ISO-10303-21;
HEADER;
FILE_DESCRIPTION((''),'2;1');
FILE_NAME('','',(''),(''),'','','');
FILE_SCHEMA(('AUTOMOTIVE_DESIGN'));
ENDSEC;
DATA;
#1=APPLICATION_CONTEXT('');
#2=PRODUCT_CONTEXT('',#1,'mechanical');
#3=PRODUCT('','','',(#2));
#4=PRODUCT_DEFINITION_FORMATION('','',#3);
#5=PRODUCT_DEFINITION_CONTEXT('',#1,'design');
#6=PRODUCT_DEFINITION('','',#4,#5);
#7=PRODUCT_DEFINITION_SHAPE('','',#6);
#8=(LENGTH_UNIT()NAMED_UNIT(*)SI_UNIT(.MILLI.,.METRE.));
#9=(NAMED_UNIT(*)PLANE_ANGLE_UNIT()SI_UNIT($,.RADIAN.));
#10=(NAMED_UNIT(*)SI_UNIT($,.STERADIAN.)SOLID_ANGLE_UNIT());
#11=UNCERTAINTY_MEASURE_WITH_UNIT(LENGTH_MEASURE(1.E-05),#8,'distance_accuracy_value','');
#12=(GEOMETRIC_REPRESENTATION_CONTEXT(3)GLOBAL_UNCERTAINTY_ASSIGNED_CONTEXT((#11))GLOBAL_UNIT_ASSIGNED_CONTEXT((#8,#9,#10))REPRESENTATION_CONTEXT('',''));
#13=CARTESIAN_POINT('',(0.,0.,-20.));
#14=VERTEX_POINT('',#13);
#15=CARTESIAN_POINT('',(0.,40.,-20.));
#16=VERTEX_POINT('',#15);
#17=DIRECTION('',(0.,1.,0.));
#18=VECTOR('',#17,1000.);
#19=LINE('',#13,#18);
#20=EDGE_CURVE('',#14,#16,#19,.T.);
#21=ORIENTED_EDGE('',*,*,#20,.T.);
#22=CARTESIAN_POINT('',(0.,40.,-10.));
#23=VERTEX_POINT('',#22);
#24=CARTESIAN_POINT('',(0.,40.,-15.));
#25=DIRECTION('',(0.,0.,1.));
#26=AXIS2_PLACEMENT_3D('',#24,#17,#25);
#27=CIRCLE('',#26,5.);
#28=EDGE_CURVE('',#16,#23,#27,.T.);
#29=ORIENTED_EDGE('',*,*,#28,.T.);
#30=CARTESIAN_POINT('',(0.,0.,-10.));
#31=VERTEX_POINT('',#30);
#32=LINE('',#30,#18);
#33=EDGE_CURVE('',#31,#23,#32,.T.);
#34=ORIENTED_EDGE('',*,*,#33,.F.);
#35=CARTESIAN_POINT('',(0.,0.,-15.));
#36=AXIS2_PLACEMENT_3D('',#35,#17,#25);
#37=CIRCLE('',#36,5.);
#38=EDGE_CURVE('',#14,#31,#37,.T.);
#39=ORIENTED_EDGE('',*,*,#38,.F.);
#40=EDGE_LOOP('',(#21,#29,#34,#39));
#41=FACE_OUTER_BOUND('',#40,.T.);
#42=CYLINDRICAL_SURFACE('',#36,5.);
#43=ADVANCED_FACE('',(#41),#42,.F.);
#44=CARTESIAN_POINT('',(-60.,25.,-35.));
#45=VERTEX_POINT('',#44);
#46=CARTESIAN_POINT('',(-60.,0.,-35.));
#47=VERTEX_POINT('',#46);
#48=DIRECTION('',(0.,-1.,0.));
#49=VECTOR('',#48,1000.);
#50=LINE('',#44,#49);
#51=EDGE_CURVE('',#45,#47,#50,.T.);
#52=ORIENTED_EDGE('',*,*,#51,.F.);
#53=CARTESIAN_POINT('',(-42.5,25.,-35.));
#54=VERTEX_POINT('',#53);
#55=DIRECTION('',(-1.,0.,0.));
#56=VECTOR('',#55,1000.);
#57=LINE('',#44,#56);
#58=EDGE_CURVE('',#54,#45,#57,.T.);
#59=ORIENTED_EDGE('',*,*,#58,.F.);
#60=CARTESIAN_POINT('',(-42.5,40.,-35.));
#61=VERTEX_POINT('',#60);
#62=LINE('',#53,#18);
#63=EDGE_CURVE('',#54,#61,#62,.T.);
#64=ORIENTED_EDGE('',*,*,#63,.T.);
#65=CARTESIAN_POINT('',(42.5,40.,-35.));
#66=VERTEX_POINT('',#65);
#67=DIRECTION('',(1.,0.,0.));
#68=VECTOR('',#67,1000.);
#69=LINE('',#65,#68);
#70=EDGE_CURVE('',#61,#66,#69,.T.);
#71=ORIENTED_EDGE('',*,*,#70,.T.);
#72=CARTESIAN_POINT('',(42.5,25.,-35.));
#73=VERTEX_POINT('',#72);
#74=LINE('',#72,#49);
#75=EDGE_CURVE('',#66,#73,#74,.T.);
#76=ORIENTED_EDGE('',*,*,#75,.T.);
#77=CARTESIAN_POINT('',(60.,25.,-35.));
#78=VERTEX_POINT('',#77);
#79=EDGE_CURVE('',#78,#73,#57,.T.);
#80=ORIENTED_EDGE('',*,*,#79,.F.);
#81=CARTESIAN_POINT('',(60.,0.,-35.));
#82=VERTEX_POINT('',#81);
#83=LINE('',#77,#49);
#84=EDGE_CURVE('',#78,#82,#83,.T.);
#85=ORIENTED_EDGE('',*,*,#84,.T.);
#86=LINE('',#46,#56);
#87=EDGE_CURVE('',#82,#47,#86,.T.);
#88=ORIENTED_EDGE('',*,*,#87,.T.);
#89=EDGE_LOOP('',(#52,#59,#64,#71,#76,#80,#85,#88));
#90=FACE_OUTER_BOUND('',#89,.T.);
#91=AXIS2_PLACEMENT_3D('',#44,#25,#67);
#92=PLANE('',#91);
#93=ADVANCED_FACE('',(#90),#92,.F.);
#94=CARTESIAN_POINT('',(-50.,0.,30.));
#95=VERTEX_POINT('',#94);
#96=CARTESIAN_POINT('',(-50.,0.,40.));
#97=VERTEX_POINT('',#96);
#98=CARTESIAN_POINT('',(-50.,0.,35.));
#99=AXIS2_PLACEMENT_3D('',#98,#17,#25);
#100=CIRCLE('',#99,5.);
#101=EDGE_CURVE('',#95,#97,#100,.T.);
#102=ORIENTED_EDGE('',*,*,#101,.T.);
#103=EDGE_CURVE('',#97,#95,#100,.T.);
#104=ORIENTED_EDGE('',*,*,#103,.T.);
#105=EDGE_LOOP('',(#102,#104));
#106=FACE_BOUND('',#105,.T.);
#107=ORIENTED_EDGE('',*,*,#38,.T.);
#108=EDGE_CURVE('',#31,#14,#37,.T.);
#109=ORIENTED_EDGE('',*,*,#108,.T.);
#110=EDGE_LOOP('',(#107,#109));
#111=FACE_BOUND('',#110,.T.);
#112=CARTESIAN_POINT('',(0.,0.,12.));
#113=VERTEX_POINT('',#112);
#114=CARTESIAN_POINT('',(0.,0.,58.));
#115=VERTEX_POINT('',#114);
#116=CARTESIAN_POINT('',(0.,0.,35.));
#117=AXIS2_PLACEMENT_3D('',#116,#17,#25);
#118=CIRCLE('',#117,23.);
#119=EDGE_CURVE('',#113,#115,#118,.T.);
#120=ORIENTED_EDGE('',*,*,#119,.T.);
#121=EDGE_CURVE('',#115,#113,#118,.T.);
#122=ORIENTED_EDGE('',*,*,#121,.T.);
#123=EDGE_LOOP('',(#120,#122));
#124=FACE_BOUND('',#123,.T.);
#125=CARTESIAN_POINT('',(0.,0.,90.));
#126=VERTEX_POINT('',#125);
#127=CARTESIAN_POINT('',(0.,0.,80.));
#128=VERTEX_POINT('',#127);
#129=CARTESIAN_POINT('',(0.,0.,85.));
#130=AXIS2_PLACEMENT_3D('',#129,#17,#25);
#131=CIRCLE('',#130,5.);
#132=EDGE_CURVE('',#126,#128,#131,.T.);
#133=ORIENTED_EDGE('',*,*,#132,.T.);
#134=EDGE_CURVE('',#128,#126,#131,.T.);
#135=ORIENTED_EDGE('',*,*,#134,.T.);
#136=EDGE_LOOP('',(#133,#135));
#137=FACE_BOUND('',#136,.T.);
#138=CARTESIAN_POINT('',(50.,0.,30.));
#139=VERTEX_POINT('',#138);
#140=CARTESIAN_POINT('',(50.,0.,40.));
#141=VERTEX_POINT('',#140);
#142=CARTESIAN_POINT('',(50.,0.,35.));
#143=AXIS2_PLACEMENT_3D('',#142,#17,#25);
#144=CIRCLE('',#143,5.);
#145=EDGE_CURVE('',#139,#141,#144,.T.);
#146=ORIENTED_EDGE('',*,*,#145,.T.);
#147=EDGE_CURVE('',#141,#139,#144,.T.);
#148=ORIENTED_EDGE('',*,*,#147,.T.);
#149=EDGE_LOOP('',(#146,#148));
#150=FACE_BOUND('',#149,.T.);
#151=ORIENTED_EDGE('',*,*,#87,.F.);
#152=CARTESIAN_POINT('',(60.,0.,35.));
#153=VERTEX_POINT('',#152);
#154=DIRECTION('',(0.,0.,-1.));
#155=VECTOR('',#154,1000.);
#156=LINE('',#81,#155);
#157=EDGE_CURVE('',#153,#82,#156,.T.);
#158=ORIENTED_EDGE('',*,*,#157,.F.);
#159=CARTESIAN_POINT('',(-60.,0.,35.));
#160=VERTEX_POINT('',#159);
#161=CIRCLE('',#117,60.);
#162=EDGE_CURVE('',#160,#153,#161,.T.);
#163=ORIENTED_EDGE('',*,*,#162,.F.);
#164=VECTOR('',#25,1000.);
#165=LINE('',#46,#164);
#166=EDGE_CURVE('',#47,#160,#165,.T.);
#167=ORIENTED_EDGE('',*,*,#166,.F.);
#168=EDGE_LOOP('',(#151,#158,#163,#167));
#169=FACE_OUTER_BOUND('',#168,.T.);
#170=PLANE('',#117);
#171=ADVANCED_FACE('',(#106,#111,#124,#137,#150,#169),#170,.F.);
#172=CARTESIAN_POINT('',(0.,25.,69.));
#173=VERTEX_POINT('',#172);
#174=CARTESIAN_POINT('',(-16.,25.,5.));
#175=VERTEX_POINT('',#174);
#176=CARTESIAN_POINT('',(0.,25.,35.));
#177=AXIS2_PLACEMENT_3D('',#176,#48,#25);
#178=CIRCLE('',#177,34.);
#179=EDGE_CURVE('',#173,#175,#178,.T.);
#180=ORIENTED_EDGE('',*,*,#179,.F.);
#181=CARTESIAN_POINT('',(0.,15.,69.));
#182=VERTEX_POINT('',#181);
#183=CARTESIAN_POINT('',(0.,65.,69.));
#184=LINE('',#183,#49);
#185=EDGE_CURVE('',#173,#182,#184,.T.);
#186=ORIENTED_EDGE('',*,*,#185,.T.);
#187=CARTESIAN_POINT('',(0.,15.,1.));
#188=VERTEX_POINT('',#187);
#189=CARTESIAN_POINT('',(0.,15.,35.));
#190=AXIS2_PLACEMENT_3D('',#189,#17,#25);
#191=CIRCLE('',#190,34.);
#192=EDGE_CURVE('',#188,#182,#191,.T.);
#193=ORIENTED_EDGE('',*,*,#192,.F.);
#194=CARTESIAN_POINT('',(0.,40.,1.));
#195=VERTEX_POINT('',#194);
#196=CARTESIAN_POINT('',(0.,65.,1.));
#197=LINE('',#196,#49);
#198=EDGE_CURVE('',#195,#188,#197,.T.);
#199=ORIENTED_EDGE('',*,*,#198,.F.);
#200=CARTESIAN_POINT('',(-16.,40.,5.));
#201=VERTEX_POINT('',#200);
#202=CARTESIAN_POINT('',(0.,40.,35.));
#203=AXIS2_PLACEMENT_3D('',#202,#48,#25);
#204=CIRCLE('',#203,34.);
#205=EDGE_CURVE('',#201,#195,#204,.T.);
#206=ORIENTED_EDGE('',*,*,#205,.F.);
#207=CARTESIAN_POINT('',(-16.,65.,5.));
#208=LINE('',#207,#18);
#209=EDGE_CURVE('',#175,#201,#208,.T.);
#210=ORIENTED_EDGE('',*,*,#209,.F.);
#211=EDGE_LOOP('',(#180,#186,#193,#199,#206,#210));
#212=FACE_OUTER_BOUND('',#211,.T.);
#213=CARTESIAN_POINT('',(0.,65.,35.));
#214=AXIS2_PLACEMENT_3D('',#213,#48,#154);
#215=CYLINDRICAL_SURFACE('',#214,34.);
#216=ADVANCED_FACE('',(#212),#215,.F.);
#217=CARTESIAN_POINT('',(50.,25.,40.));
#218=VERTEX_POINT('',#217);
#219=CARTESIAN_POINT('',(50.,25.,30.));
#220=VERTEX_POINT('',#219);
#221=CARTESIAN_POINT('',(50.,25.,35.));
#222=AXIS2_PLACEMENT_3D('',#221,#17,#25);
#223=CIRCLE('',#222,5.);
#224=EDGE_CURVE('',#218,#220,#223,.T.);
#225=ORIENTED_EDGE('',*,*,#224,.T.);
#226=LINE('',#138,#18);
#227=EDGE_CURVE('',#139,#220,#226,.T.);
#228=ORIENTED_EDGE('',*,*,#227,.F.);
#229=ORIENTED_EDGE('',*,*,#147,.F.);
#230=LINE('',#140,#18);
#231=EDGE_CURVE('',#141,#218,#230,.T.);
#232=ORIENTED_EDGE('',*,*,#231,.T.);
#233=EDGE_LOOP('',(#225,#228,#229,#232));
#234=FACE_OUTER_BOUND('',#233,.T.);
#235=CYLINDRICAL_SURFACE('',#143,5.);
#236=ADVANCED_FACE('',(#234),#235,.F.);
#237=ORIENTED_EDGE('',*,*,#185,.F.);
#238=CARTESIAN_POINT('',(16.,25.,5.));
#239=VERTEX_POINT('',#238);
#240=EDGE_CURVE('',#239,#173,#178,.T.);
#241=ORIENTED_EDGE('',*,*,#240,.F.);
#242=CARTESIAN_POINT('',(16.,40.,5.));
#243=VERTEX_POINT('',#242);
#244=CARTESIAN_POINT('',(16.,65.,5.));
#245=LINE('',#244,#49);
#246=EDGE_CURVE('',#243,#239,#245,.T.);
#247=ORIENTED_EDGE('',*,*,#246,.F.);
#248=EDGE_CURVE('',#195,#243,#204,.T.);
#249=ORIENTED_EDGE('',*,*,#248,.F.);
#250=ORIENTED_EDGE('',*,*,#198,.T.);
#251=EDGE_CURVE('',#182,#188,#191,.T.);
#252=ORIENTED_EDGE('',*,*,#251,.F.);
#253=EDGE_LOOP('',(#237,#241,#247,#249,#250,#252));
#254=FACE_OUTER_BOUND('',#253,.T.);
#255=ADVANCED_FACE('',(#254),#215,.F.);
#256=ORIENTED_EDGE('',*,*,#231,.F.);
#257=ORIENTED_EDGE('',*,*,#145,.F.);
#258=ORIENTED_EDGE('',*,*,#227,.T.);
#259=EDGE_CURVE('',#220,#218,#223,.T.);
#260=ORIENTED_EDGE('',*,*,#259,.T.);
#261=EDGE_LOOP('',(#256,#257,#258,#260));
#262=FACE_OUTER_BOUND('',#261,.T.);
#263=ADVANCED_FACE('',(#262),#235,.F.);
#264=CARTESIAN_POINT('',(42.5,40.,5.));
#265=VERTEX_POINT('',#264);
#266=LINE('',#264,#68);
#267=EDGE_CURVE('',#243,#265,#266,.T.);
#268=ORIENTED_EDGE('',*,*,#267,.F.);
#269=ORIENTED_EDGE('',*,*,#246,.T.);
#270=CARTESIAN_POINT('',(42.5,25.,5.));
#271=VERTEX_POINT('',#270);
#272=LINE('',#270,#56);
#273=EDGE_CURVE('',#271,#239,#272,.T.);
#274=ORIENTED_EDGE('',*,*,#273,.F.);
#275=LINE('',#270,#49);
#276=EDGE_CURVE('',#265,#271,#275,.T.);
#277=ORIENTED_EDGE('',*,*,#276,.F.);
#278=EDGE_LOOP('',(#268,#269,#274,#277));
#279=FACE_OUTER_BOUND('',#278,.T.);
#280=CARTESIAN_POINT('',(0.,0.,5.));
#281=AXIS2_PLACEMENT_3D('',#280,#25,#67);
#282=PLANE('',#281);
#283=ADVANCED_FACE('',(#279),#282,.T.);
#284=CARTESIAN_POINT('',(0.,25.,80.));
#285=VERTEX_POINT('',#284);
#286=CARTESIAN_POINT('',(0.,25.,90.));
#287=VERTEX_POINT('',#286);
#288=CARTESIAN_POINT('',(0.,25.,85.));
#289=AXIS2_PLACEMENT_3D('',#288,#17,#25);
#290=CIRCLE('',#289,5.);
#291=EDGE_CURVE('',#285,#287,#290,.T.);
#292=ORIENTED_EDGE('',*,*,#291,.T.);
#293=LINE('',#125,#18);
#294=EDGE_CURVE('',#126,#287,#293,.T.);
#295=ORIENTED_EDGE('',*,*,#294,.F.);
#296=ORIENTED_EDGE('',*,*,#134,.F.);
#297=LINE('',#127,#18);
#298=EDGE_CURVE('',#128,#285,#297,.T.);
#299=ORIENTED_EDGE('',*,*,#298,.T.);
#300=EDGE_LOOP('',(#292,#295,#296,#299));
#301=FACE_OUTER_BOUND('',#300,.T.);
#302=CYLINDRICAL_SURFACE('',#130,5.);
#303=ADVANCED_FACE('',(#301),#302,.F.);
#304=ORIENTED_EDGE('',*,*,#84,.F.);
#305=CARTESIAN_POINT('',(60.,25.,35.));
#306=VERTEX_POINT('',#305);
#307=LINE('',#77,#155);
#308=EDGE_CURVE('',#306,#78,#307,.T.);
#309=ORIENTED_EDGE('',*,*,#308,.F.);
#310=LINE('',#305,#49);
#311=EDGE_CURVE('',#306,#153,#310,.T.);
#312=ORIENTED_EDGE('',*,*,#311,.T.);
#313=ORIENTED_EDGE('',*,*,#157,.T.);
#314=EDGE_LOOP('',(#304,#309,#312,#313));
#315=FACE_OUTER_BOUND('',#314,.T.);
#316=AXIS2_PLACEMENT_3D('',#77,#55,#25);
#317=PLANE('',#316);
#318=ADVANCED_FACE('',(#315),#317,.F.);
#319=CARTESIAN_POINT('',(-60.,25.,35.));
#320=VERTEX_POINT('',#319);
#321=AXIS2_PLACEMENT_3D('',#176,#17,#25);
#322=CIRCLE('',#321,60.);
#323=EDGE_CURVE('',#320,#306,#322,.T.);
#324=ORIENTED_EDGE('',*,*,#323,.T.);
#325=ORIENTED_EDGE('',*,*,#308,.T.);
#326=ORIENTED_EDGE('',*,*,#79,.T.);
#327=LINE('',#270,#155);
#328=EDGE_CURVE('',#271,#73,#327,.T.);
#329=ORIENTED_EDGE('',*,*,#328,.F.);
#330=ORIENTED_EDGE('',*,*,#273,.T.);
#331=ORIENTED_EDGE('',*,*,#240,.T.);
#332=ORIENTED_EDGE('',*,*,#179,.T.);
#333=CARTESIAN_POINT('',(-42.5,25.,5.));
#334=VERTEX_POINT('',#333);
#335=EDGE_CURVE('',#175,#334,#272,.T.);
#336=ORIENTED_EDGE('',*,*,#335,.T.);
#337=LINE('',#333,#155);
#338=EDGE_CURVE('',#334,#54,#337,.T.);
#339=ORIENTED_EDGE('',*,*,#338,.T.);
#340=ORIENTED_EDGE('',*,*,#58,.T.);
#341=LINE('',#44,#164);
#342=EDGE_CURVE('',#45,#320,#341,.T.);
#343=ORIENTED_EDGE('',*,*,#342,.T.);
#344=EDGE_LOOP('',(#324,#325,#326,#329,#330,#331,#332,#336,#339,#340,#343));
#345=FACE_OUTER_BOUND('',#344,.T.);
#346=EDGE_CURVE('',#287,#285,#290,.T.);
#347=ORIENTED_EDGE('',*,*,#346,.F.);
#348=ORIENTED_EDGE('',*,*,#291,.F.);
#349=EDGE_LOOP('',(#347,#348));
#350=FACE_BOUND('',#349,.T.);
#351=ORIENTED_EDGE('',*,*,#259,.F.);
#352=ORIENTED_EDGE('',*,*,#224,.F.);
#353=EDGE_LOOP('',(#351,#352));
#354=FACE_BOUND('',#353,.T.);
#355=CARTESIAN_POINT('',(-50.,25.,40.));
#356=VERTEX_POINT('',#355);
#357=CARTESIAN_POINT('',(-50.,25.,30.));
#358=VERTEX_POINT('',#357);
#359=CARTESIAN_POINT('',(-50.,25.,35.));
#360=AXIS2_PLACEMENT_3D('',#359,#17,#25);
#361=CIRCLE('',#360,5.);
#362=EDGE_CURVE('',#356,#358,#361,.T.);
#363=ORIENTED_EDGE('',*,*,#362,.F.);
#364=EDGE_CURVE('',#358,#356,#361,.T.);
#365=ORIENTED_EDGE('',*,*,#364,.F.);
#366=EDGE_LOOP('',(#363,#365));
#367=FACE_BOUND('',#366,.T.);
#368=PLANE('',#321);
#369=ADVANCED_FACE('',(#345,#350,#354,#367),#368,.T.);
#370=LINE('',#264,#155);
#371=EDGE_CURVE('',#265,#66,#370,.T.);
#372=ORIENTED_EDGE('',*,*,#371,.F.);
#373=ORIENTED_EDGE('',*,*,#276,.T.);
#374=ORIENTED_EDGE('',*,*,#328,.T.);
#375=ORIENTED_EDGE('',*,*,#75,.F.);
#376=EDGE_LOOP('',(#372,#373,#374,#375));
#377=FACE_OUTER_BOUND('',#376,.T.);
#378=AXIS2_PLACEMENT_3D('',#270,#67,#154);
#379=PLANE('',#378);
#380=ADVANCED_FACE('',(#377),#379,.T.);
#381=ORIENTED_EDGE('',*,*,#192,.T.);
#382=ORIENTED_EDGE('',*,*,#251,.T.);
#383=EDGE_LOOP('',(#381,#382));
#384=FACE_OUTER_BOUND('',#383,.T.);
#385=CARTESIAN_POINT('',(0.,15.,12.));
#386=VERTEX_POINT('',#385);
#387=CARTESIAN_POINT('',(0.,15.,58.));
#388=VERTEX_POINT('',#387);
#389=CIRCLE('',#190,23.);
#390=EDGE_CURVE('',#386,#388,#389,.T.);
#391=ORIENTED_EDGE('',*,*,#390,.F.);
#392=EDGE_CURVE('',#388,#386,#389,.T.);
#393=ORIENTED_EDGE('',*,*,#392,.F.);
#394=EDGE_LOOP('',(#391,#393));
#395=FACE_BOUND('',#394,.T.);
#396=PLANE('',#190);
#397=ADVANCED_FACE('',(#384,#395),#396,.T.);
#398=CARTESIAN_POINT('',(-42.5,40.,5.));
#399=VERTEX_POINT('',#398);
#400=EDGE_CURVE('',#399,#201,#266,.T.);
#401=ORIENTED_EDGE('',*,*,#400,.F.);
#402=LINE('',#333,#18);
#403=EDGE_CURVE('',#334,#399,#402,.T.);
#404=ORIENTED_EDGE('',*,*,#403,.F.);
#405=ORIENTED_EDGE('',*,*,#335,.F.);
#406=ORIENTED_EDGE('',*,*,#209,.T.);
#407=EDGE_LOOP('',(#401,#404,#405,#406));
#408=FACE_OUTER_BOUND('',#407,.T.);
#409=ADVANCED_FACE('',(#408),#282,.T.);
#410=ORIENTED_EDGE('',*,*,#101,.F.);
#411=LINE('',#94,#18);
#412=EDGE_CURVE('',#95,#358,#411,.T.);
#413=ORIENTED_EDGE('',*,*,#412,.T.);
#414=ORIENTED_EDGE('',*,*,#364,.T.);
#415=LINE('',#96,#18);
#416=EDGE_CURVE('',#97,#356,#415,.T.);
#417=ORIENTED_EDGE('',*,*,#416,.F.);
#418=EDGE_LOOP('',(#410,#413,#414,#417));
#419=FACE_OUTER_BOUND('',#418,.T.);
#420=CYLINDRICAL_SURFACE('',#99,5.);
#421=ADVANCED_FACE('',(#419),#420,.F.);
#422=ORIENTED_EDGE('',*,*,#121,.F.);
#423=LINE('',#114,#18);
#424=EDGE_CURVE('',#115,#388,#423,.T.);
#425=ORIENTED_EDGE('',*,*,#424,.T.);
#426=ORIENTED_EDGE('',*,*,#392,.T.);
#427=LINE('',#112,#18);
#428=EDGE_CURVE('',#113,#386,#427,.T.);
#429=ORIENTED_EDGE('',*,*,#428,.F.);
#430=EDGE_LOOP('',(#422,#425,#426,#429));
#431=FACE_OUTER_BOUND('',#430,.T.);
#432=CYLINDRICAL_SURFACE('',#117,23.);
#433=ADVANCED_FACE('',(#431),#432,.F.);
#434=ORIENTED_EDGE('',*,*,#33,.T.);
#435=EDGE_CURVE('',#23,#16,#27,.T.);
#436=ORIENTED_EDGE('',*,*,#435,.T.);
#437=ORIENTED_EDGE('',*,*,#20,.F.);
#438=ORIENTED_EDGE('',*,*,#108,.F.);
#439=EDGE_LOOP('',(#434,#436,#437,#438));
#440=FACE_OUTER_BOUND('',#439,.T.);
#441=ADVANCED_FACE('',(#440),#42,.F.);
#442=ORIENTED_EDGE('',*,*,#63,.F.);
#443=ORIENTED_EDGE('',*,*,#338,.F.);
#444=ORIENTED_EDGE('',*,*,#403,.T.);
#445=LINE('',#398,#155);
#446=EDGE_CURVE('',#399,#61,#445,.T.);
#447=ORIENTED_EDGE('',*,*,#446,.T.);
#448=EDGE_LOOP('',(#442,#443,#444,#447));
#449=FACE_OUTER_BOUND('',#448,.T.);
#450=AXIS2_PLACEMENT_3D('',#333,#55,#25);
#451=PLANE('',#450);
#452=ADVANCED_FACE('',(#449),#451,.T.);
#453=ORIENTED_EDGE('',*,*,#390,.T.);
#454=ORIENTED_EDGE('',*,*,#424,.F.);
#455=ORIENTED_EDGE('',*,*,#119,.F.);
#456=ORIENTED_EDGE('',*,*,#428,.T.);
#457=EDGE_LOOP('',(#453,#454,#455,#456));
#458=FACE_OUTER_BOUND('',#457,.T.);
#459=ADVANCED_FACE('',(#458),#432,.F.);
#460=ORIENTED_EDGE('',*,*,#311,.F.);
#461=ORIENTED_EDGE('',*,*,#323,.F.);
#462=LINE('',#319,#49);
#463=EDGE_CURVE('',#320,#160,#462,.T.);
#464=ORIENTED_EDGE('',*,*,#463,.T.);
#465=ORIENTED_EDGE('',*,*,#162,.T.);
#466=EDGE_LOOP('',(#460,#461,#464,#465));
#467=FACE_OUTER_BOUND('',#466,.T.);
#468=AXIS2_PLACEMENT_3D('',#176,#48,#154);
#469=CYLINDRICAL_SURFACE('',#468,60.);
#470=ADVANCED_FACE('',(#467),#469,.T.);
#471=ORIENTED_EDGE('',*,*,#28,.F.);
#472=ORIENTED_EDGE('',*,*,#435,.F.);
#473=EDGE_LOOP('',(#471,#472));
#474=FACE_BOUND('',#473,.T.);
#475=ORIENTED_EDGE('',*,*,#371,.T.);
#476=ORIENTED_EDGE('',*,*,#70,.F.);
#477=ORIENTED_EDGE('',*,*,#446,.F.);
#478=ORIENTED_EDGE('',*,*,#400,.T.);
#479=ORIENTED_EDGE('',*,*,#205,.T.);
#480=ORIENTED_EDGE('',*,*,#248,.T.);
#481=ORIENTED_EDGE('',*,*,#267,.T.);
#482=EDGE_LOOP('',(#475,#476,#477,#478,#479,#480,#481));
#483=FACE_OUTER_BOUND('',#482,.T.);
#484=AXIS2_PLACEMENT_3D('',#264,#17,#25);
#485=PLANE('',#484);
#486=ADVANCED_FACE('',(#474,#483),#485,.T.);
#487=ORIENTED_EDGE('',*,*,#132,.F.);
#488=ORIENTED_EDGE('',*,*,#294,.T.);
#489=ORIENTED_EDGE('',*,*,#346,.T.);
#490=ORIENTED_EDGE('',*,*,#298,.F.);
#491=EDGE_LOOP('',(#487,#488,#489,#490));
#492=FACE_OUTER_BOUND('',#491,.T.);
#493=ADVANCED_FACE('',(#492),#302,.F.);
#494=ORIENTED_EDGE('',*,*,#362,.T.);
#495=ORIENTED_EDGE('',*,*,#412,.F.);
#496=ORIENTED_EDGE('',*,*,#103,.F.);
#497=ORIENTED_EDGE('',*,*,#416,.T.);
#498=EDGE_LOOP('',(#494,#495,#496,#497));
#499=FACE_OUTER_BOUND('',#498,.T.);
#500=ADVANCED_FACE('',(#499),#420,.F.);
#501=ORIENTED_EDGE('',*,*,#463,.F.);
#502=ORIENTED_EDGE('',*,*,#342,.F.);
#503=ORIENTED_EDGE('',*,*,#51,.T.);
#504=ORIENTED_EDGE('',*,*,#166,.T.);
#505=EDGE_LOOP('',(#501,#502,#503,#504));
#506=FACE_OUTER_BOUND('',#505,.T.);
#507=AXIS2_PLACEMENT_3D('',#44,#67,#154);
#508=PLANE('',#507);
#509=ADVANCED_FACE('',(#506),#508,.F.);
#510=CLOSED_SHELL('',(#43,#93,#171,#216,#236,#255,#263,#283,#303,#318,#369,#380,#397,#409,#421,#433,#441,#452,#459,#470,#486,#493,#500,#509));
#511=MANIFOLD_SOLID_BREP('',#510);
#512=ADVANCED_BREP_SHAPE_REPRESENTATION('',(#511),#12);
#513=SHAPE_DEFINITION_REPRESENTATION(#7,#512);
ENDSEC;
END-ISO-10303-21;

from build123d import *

# Parameters (mm, degrees)
BASE_PLATE_DEPTH          = 25
UPRIGHT_BLOCK_SKETCH_W    = 85
UPRIGHT_BLOCK_SKETCH_H    = 15
UPRIGHT_BLOCK_DEPTH       = 40
MOUNTING_HOLES_SKETCH_R   = 5
MOUNTING_HOLES_CUT_DEPTH  = 40
COUNTERBORE_68_DEPTH      = 40
COUNTERBORE_68_DEPTH_BACK = 10
COUNTERBORE_68_SKETCH_R   = 34
BORE_46_SKETCH_R          = 23
BORE_46_DEPTH             = 15


with BuildPart() as part:
    # Base Plate Sketch → Base Plate (new body)
    with BuildSketch(Plane(origin=(0, 0, 0), x_dir=(1, 0, 0), z_dir=(0, 1, 0))):
        with BuildLine():
            Line((-60, 35), (60, 35))
            Line((60, 35), (60, -35))
            ThreePointArc((60, -35), (0, -95), (-60, -35))
            Line((-60, -35), (-60, 35))
        make_face()
    extrude(amount=BASE_PLATE_DEPTH)

    # Upright Block Sketch → Upright Block (add)
    with BuildSketch(Plane(origin=(0, 0, -35), x_dir=(-1, 0, 0), z_dir=(0, 0, -1))):
        with Locations((0, 32.5)):
            Rectangle(UPRIGHT_BLOCK_SKETCH_W, UPRIGHT_BLOCK_SKETCH_H)
    extrude(amount=-UPRIGHT_BLOCK_DEPTH)

    # Mounting Holes Sketch → Mounting Holes Cut (cut)
    with BuildSketch(Plane(origin=(0, 40, 0), x_dir=(1, 0, 0), z_dir=(0, 1, 0))):
        with Locations(Location((0, 15, 0), (0, 0, 270))):
            Circle(MOUNTING_HOLES_SKETCH_R)
        with Locations(Location((-50, -35, 0), (0, 0, 270))):
            Circle(MOUNTING_HOLES_SKETCH_R)
        with Locations(Location((50, -35, 0), (0, 0, 270))):
            Circle(MOUNTING_HOLES_SKETCH_R)
        with Locations(Location((0, -85, 0), (0, 0, 270))):
            Circle(MOUNTING_HOLES_SKETCH_R)
    extrude(amount=-MOUNTING_HOLES_CUT_DEPTH, mode=Mode.SUBTRACT)

    # Counterbore Ø68 Sketch → Counterbore Ø68 (cut, two sides: drawn at the far end of the back side and taken through both)
    with BuildSketch(Plane(origin=(0, 25, 0), x_dir=(1, 0, 0), z_dir=(0, 1, 0)).offset(-COUNTERBORE_68_DEPTH_BACK)):
        with Locations(Location((0, -35, 0), (0, 0, 61.927513064))):
            Circle(COUNTERBORE_68_SKETCH_R)
    extrude(amount=COUNTERBORE_68_DEPTH + COUNTERBORE_68_DEPTH_BACK, mode=Mode.SUBTRACT)

    # Bore Ø46 Sketch → Bore Ø46 (cut)
    with BuildSketch(Plane(origin=(0, 15, 0), x_dir=(1, 0, 0), z_dir=(0, 1, 0))):
        with Locations(Location((0, -35, 0), (0, 0, 270))):
            Circle(BORE_46_SKETCH_R)
    extrude(amount=-BORE_46_DEPTH, mode=Mode.SUBTRACT)


solid = part.part
